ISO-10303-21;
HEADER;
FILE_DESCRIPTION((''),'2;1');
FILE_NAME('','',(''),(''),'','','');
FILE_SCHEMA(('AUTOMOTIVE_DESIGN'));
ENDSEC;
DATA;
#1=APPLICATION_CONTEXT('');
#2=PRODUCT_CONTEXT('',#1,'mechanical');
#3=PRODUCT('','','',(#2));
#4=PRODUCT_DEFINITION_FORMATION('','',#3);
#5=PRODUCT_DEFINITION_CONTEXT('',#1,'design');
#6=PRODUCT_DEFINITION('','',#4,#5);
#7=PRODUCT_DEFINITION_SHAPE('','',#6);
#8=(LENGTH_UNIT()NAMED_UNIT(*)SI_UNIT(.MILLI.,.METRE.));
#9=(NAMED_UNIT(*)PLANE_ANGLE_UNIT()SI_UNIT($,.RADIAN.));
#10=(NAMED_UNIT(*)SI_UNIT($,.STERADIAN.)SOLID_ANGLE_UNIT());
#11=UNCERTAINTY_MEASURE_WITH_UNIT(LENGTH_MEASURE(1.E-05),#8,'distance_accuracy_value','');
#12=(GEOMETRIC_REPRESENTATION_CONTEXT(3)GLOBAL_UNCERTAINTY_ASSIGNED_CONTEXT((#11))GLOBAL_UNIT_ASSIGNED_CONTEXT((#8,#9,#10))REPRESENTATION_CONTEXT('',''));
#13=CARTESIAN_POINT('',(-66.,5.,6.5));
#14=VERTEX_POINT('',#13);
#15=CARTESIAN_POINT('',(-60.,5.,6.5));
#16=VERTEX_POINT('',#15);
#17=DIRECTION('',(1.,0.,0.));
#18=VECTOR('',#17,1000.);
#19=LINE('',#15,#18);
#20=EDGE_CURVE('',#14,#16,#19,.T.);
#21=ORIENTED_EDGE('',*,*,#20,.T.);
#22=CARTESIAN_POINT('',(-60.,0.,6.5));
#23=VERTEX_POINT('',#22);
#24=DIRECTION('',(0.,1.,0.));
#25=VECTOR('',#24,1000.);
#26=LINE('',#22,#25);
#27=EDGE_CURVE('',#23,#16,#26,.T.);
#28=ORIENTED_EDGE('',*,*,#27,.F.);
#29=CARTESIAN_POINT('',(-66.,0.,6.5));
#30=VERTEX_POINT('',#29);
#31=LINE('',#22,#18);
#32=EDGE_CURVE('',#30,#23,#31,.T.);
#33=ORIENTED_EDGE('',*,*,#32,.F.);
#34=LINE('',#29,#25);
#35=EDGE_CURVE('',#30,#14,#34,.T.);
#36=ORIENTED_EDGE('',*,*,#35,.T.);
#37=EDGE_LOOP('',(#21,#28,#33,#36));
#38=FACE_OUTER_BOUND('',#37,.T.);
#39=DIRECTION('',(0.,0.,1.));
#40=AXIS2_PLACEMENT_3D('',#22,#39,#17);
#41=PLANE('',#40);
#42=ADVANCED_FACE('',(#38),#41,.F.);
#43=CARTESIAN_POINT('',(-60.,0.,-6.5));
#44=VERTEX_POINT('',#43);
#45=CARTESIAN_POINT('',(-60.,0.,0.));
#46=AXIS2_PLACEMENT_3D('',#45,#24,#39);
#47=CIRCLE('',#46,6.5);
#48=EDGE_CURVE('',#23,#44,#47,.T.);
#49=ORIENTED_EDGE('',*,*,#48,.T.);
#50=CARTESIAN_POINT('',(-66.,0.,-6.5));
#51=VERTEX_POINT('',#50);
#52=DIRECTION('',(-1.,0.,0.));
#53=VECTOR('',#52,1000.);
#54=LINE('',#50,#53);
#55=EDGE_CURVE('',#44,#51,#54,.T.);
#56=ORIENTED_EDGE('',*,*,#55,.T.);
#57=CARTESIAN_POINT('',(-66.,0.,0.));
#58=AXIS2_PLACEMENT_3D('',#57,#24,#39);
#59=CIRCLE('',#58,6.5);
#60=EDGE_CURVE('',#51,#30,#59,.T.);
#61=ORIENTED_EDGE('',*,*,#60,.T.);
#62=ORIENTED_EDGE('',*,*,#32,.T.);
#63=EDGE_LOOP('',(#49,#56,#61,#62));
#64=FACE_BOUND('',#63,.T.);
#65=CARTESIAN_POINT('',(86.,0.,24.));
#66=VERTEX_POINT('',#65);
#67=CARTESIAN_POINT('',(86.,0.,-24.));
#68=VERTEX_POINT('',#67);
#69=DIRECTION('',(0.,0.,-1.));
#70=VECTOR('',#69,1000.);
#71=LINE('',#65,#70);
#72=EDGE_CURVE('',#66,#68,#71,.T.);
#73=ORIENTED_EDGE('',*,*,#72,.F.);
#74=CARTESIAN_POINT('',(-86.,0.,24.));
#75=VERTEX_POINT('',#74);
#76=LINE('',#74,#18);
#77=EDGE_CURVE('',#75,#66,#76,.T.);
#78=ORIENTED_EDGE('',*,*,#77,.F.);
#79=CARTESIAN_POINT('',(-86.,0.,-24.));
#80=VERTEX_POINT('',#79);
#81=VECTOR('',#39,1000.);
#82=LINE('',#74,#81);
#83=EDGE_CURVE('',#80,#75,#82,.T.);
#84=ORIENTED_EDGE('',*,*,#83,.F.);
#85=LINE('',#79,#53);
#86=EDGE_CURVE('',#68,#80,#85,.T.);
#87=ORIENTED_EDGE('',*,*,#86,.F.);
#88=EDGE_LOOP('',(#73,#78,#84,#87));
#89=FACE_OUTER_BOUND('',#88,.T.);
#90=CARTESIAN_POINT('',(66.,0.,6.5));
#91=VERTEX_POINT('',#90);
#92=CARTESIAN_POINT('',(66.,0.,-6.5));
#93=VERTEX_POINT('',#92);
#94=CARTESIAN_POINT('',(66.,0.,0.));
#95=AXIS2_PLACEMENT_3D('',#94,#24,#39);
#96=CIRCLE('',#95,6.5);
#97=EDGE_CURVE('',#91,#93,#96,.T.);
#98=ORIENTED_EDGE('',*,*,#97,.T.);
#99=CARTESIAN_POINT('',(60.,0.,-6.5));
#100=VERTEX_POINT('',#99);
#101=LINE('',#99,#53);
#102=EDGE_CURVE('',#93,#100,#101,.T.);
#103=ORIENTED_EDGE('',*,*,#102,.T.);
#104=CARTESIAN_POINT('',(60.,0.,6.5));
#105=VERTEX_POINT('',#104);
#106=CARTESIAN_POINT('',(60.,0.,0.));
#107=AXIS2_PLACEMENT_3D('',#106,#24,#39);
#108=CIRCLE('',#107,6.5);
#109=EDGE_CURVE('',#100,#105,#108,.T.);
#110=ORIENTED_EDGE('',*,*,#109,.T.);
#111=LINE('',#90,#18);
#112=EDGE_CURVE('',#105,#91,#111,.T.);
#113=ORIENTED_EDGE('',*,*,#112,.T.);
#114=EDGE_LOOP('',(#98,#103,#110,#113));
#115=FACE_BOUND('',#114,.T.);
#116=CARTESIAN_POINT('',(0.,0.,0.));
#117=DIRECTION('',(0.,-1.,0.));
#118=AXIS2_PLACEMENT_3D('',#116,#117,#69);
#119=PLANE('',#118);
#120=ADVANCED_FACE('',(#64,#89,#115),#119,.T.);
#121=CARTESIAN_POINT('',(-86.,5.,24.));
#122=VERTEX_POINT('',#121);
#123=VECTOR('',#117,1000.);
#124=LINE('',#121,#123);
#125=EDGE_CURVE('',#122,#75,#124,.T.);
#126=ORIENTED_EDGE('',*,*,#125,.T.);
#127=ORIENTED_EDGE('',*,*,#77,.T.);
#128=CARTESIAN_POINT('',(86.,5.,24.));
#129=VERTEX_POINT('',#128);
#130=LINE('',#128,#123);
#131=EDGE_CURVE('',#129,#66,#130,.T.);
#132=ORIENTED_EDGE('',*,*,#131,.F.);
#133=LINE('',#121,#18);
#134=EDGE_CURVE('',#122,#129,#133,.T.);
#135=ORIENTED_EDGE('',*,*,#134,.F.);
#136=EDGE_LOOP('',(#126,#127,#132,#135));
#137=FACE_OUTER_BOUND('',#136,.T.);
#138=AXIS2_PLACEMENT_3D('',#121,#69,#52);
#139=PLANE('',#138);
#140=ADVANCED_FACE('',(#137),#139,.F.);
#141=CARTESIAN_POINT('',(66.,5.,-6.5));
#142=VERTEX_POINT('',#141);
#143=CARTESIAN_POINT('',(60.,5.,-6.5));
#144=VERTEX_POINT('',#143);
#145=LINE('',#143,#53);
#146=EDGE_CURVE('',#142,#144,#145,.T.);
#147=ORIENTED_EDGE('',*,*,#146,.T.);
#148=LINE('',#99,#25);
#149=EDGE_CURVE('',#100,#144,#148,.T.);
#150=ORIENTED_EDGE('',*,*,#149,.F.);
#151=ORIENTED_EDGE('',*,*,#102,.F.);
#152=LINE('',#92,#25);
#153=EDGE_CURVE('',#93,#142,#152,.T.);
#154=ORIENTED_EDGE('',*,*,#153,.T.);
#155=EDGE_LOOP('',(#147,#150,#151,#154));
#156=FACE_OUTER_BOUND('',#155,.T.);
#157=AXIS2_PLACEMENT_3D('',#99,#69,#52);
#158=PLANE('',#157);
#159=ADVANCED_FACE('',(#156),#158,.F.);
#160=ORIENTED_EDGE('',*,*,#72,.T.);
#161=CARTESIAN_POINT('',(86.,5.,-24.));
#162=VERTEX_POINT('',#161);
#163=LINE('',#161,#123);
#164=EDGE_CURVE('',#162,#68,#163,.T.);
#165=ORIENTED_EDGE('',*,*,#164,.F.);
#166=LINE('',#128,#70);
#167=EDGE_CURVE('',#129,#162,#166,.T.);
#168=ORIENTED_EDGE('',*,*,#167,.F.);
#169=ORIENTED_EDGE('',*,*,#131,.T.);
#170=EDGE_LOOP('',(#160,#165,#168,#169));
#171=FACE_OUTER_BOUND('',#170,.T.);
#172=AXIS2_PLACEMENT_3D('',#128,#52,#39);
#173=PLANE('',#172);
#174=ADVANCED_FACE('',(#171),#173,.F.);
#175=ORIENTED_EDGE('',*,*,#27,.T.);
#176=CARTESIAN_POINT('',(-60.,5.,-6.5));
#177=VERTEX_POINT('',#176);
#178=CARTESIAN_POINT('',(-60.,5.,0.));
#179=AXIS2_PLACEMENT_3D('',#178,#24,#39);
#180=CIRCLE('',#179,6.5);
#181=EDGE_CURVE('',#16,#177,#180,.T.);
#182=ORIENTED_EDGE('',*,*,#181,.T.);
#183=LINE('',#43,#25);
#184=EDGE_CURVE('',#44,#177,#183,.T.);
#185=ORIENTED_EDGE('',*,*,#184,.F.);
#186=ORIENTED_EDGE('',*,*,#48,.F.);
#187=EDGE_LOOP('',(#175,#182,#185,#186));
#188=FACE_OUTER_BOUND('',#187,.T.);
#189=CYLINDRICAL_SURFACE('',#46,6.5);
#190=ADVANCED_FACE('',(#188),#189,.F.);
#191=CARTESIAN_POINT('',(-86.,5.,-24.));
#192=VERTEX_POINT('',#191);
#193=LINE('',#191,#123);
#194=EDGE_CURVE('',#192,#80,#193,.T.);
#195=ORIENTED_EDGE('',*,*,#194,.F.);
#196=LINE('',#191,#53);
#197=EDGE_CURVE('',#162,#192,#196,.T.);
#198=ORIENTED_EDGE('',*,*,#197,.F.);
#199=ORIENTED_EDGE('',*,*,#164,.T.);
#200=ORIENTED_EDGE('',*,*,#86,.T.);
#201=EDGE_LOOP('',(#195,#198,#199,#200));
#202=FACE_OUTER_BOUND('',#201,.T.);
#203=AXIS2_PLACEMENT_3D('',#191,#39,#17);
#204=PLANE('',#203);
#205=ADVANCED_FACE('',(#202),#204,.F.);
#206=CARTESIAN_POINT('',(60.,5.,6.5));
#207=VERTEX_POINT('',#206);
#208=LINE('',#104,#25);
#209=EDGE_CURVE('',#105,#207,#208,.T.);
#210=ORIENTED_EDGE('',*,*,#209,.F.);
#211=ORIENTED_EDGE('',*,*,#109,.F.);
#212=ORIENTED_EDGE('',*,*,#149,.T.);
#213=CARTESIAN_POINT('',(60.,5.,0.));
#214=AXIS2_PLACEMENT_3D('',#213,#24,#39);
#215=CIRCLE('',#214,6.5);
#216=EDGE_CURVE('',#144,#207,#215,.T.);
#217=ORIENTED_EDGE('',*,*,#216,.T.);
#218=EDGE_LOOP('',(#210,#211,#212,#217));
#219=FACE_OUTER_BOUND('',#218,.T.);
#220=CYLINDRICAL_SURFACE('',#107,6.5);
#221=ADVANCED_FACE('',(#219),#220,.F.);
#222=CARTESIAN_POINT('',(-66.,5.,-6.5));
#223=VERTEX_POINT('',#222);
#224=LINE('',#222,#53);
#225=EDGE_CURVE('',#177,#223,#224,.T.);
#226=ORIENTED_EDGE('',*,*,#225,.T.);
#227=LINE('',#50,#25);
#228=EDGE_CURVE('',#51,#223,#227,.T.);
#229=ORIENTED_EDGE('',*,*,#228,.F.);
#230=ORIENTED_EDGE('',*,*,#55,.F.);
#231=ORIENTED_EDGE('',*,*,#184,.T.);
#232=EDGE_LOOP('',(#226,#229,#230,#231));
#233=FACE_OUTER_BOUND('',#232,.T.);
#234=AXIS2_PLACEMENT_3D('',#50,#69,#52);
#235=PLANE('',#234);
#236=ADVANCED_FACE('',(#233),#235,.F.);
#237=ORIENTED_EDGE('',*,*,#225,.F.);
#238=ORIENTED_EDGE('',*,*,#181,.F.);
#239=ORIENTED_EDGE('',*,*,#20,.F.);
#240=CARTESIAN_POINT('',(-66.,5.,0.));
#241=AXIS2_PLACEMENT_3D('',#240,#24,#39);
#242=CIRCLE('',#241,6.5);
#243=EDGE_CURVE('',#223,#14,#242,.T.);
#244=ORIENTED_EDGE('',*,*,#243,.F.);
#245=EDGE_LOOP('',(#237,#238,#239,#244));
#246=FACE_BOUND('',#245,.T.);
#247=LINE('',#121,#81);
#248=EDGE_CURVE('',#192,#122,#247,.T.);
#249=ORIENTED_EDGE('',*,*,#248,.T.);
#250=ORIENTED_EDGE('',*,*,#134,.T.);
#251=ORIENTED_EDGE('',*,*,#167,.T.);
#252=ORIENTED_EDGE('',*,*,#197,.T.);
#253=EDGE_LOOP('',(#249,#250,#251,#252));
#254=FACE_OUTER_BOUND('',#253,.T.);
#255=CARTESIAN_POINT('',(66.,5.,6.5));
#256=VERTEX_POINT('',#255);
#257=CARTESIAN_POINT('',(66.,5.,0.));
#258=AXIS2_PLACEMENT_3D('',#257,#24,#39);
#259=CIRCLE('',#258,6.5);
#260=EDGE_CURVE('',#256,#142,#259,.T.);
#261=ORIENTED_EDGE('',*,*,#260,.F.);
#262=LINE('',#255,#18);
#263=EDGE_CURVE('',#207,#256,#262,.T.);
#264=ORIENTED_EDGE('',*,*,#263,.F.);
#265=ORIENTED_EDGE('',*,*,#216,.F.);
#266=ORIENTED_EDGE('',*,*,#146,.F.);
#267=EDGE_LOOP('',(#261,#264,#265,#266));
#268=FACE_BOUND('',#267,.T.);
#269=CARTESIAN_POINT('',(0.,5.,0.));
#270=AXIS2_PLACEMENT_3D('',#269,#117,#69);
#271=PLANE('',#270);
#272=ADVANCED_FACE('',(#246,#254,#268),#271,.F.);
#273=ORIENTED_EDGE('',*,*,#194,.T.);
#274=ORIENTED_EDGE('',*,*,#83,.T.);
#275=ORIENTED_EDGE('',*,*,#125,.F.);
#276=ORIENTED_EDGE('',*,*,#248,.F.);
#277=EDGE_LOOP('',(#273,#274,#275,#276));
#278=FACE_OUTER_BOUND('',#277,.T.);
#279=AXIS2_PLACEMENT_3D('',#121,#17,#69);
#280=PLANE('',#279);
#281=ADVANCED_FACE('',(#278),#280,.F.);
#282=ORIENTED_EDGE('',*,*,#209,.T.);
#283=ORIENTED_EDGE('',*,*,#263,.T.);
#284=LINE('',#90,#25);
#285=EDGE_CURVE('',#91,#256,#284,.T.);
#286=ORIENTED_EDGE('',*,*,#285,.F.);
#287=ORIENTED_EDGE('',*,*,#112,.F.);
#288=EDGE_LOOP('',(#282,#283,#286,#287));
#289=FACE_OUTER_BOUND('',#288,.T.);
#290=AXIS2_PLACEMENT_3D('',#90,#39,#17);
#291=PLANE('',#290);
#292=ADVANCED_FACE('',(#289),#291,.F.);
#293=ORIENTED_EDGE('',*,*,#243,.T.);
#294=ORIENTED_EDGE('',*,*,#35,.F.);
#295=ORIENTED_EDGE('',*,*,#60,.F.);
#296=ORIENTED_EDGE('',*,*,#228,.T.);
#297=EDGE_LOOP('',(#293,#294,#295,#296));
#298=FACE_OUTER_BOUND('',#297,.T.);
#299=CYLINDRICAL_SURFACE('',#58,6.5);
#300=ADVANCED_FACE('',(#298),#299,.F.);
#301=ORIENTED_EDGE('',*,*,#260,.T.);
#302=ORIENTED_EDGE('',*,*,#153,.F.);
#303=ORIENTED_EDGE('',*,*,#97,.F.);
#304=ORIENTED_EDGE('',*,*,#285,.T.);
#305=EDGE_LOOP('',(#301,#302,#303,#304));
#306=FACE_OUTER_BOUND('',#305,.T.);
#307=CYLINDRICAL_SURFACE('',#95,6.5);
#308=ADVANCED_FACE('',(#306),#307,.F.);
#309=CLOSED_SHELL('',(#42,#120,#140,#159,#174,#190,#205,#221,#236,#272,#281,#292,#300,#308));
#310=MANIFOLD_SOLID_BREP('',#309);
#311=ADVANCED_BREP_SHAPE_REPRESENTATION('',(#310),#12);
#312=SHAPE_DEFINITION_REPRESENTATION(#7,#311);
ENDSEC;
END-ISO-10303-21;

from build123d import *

# Parameters (mm, degrees)
SKETCH_1_W          = 172
SKETCH_1_H          = 48
EXTRUDE_1_DEPTH     = 5
CUT_EXTRUDE_1_DEPTH = 90.425947018


with BuildPart() as part:
    # 草图1 → 凸台-拉伸1 (new body)
    with BuildSketch(Plane(origin=(0, 0, 0), x_dir=(1, 0, 0), z_dir=(0, 1, 0))):
        Rectangle(SKETCH_1_W, SKETCH_1_H)
    extrude(amount=EXTRUDE_1_DEPTH)

    # 草图2 → 切除-拉伸1 (cut, through all)
    with BuildSketch(Plane(origin=(0, 5, 0), x_dir=(1, 0, 0), z_dir=(0, 1, 0))):
        with BuildLine():
            Line((66, -6.5), (60, -6.5))
            ThreePointArc((60, -6.5), (53.5, 0), (60, 6.5))
            Line((60, 6.5), (66, 6.5))
            ThreePointArc((66, 6.5), (72.5, 0), (66, -6.5))
        make_face()
        with BuildLine():
            Line((-66, 6.5), (-60, 6.5))
            ThreePointArc((-60, 6.5), (-53.5, 0), (-60, -6.5))
            Line((-60, -6.5), (-66, -6.5))
            ThreePointArc((-66, -6.5), (-72.5, 0), (-66, 6.5))
        make_face()
    extrude(amount=-CUT_EXTRUDE_1_DEPTH, mode=Mode.SUBTRACT)


solid = part.part
